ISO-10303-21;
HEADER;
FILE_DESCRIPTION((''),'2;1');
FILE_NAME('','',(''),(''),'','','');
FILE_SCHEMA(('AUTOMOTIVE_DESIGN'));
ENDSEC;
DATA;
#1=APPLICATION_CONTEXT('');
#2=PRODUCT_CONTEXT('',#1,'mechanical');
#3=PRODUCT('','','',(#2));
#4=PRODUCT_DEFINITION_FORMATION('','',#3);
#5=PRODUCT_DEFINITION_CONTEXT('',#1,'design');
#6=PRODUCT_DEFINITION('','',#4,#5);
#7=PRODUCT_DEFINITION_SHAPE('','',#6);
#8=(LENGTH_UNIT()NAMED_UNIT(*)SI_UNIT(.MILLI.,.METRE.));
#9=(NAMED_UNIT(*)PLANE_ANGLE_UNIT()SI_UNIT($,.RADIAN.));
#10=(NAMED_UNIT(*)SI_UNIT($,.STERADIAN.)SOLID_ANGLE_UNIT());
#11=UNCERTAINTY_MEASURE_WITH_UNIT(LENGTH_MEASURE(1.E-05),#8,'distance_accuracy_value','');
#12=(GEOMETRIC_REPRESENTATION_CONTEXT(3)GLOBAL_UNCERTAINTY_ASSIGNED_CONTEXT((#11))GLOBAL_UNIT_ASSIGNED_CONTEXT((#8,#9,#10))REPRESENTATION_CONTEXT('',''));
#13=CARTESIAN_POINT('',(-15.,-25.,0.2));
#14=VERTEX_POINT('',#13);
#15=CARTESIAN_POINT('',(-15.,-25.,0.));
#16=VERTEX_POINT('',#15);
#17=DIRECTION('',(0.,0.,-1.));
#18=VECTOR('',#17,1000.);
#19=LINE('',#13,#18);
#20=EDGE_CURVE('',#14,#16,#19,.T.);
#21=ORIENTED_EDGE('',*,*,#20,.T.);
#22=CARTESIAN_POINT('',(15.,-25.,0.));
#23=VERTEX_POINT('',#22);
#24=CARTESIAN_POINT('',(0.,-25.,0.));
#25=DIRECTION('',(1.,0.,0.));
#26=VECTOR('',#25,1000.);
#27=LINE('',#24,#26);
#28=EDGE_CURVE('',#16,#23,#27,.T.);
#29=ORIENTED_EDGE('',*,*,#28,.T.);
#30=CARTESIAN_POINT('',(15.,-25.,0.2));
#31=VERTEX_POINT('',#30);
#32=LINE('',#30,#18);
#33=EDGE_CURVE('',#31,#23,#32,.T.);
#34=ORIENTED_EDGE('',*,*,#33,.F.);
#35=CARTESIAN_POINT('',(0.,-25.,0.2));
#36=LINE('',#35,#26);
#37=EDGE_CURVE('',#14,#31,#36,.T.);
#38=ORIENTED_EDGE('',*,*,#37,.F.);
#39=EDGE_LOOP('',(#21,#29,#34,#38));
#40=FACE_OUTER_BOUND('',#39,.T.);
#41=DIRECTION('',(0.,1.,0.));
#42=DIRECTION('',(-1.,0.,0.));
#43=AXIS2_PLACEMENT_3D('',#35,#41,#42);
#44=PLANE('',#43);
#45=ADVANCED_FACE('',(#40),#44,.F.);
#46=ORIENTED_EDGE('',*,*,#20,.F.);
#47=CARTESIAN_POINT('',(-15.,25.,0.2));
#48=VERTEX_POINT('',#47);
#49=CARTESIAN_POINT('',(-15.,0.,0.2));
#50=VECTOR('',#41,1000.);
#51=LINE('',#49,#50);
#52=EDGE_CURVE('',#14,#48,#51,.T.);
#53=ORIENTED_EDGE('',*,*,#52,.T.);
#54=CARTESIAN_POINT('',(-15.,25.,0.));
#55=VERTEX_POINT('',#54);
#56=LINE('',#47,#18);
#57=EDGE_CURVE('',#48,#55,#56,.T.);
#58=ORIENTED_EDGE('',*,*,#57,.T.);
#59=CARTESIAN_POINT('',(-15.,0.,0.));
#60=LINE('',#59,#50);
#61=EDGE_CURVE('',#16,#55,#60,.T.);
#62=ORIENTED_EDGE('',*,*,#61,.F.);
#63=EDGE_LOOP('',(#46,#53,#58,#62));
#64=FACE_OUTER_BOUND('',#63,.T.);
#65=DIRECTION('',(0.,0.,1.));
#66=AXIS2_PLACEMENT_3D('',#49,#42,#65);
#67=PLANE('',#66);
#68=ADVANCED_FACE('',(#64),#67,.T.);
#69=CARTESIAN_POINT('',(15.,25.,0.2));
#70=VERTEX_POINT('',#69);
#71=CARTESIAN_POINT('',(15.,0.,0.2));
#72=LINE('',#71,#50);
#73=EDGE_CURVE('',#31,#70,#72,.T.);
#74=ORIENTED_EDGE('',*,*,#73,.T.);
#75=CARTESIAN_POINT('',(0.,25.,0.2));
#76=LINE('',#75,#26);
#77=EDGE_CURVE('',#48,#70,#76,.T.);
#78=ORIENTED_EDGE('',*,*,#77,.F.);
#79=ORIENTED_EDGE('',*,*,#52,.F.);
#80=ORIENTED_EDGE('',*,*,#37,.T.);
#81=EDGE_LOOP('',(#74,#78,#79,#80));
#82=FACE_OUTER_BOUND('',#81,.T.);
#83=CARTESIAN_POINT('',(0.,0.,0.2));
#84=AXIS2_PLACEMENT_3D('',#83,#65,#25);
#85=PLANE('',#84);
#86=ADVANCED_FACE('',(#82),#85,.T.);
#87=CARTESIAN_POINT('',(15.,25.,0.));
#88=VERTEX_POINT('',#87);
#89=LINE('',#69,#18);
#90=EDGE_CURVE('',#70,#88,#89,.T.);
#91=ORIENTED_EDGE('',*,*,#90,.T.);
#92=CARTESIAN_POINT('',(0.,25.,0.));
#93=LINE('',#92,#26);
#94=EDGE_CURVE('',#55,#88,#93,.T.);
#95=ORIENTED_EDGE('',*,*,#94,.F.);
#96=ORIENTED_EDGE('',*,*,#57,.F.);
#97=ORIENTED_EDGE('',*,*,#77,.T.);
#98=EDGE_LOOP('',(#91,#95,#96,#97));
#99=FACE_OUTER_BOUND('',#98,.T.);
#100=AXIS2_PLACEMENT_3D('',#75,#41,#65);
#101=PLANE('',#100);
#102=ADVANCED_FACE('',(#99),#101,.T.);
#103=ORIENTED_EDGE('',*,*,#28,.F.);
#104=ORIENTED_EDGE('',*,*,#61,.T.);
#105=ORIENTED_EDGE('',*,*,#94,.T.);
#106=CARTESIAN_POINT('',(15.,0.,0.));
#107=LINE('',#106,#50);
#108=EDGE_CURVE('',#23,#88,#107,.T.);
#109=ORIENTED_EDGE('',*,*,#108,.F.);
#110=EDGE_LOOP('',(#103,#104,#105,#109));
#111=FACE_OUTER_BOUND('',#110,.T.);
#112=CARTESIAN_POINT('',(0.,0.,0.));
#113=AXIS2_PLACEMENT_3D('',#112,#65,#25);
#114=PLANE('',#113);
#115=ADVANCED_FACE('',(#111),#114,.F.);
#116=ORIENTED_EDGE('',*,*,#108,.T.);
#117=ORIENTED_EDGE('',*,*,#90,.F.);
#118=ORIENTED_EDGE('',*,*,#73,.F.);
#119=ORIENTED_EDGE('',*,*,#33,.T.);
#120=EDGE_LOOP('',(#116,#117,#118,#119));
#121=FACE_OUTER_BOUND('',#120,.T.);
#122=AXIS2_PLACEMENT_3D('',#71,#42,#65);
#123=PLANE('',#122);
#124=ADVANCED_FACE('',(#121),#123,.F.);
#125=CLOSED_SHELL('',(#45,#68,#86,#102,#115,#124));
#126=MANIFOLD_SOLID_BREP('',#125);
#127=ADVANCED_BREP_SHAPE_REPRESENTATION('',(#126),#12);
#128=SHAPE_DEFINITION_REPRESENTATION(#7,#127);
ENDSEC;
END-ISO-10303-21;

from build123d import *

# Parameters (mm, degrees)
SKETCH_1_W      = 30
SKETCH_1_H      = 50
EXTRUDE_1_DEPTH = 0.2


with BuildPart() as part:
    # 草图1 → 凸台-拉伸1 (new body)
    with BuildSketch(Plane.XY):
        Rectangle(SKETCH_1_W, SKETCH_1_H)
    extrude(amount=EXTRUDE_1_DEPTH)


solid = part.part
